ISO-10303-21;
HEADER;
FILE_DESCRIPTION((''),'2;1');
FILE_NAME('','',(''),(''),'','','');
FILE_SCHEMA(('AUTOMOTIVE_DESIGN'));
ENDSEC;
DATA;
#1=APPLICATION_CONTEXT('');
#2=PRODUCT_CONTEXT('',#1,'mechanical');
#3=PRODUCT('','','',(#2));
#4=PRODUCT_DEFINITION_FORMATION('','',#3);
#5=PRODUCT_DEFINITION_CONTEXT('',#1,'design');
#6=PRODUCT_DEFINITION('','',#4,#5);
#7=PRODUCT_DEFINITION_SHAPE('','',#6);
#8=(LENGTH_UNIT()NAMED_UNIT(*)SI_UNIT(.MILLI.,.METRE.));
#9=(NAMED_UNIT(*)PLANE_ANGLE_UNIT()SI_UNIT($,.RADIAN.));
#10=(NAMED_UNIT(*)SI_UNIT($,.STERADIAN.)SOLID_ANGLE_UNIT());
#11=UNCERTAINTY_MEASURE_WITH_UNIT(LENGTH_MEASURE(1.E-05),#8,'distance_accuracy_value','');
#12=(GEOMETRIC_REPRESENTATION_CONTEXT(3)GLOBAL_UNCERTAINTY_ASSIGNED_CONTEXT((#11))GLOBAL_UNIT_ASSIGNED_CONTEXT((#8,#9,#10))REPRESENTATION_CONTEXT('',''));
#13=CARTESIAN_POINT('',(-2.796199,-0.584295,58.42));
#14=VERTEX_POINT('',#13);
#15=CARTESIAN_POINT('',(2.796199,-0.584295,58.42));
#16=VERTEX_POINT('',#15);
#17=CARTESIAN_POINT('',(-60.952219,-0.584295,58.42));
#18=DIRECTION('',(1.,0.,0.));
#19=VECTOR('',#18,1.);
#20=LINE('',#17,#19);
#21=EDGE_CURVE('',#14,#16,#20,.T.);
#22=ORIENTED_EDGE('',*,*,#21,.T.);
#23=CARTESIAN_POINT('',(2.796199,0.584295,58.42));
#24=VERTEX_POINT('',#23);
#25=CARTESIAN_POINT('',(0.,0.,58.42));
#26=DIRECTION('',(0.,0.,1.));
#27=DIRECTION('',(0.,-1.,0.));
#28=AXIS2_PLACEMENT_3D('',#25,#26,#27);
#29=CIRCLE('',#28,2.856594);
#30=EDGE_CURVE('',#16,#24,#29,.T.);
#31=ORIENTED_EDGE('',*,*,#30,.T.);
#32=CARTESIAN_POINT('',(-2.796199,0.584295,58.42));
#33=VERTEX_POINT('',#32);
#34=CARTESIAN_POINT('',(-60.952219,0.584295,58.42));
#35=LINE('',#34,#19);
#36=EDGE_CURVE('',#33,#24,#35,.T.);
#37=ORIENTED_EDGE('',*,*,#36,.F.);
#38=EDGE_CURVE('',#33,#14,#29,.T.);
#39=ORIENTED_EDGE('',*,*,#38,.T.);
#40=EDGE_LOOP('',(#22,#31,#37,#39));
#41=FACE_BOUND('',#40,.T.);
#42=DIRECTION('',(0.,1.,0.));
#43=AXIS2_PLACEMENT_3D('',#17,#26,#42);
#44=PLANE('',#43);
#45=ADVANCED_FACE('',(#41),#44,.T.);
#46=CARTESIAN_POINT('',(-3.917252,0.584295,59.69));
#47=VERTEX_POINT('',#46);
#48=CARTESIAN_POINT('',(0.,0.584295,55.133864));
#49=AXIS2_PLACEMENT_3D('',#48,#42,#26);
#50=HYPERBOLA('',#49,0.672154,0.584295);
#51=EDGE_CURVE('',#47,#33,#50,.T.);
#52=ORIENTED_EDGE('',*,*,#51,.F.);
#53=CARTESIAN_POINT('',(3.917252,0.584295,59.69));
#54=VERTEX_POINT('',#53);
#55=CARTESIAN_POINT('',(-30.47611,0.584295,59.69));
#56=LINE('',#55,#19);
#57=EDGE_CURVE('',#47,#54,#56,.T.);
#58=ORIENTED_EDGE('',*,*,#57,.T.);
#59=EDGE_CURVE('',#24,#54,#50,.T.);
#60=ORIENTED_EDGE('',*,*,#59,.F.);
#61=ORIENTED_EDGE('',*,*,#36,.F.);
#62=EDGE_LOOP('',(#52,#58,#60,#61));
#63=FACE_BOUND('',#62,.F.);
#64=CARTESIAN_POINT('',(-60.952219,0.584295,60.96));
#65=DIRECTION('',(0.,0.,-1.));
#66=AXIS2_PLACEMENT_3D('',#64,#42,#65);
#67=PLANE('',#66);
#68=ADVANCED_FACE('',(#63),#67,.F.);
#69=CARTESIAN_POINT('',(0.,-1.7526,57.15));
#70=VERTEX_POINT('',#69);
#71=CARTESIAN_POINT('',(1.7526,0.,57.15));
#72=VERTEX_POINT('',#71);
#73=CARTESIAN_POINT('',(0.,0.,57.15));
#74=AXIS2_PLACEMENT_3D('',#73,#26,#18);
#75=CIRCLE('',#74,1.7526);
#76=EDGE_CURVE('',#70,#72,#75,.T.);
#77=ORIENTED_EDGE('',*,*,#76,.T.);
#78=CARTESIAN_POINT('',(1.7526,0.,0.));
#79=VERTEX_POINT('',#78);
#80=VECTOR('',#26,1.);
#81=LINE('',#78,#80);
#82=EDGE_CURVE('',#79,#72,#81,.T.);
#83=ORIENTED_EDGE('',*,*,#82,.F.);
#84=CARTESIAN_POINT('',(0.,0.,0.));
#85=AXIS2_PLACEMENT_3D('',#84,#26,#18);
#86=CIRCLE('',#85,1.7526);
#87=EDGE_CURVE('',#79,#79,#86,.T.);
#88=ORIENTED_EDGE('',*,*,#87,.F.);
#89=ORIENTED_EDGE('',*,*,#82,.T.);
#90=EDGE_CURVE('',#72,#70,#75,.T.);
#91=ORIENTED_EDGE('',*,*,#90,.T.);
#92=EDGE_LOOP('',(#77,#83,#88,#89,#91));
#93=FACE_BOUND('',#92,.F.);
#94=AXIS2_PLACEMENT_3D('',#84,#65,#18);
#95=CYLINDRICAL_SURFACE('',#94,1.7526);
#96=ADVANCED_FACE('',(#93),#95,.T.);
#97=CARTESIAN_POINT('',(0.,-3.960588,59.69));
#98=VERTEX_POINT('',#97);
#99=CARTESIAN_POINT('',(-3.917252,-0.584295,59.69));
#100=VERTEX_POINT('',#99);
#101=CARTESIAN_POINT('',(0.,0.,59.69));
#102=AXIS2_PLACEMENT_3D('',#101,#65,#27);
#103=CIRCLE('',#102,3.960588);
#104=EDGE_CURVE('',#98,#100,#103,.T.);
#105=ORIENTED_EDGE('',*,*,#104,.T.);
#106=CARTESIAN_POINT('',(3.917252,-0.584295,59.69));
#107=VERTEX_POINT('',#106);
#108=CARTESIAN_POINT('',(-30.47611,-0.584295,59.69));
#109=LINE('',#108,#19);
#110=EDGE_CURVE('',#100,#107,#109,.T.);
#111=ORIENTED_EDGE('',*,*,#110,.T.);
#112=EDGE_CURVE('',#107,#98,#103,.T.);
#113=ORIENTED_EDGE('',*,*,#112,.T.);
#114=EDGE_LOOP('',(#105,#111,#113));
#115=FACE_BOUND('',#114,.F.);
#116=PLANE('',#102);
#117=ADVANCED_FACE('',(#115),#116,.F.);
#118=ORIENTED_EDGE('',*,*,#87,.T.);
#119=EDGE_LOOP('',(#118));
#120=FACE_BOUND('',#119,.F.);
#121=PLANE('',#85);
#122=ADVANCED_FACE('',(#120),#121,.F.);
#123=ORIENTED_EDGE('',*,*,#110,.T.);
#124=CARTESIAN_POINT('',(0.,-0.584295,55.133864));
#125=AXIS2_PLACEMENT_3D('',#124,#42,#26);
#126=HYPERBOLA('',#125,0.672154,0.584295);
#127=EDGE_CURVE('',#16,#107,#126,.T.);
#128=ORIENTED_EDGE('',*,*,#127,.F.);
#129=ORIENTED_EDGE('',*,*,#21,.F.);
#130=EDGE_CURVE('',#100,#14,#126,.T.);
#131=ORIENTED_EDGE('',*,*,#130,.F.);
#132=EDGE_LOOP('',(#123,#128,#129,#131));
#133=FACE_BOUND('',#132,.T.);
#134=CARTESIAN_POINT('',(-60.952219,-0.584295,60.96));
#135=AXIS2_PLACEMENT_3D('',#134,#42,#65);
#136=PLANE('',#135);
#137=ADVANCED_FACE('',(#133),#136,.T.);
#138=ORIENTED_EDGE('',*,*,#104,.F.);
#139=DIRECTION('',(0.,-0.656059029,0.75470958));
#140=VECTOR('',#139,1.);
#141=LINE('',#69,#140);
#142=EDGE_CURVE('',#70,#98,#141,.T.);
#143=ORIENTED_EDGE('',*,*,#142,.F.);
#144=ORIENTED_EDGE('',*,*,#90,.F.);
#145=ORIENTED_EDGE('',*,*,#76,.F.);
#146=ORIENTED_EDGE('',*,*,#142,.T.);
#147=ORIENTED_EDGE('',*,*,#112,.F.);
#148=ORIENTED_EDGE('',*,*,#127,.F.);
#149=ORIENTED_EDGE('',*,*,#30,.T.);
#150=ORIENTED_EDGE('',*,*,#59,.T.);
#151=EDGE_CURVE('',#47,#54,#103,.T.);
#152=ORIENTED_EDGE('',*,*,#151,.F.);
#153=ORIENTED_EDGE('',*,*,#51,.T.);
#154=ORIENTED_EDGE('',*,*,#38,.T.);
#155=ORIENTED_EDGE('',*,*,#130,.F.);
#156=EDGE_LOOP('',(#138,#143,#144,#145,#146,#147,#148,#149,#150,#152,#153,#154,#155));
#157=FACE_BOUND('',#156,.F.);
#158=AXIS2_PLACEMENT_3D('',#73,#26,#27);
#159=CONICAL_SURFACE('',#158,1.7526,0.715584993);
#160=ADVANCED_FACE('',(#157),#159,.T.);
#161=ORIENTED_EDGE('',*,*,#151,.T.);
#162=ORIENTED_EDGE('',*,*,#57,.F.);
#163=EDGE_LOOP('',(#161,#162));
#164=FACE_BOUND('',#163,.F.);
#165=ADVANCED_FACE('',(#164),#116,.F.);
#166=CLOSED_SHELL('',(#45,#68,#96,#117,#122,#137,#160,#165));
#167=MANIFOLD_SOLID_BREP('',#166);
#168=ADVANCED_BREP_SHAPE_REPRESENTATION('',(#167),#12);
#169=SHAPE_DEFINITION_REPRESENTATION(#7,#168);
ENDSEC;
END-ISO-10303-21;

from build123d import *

# Parameters (mm, degrees)
SHANK_PROFILE_0_138_R       = 1.7526
SHANK_0_138_X_2_25_DEPTH    = 57.15
SCREWDRIVER_SLOT_DEPTH      = 60.952219472
SCREWDRIVER_SLOT_DEPTH_BACK = 60.952219472
SCREWDRIVER_SLOT_PROFILE_W  = 2.54
SCREWDRIVER_SLOT_PROFILE_H  = 1.168589104


with BuildPart() as part:
    # Shank Profile Ø0.138 → Shank Ø0.138 x 2.25 (new body)
    with BuildSketch(Plane.XY):
        Circle(SHANK_PROFILE_0_138_R)
    extrude(amount=SHANK_0_138_X_2_25_DEPTH)

    # Countersunk Head Profile → Countersunk Head 82° (revolve)
    with BuildSketch(Plane(origin=(0, 0, 0), x_dir=(0, 0, -1), z_dir=(1, 0, 0)), mode=Mode.PRIVATE) as countersunk_head_82_sk:
        Polygon((-57.15, 1.7526), (-59.69, 3.960588314), (-59.69, 0), (-57.15, 0), align=None)
    revolve(countersunk_head_82_sk.sketch.rotate(Axis((0, 0, 59.69), (0, 0, -1)), 180), axis=Axis((0, 0, 59.69), (0, 0, -1)))

    # Screwdriver Slot Profile → Screwdriver Slot (cut, two sides: drawn at the far end of the back side and taken through both)
    with BuildSketch(Plane(origin=(0, 0, 0), x_dir=(0, 0, -1), z_dir=(1, 0, 0)).offset(-SCREWDRIVER_SLOT_DEPTH_BACK)):
        with Locations((-59.69, 0)):
            Rectangle(SCREWDRIVER_SLOT_PROFILE_W, SCREWDRIVER_SLOT_PROFILE_H)
    extrude(amount=SCREWDRIVER_SLOT_DEPTH + SCREWDRIVER_SLOT_DEPTH_BACK, mode=Mode.SUBTRACT)


solid = part.part
